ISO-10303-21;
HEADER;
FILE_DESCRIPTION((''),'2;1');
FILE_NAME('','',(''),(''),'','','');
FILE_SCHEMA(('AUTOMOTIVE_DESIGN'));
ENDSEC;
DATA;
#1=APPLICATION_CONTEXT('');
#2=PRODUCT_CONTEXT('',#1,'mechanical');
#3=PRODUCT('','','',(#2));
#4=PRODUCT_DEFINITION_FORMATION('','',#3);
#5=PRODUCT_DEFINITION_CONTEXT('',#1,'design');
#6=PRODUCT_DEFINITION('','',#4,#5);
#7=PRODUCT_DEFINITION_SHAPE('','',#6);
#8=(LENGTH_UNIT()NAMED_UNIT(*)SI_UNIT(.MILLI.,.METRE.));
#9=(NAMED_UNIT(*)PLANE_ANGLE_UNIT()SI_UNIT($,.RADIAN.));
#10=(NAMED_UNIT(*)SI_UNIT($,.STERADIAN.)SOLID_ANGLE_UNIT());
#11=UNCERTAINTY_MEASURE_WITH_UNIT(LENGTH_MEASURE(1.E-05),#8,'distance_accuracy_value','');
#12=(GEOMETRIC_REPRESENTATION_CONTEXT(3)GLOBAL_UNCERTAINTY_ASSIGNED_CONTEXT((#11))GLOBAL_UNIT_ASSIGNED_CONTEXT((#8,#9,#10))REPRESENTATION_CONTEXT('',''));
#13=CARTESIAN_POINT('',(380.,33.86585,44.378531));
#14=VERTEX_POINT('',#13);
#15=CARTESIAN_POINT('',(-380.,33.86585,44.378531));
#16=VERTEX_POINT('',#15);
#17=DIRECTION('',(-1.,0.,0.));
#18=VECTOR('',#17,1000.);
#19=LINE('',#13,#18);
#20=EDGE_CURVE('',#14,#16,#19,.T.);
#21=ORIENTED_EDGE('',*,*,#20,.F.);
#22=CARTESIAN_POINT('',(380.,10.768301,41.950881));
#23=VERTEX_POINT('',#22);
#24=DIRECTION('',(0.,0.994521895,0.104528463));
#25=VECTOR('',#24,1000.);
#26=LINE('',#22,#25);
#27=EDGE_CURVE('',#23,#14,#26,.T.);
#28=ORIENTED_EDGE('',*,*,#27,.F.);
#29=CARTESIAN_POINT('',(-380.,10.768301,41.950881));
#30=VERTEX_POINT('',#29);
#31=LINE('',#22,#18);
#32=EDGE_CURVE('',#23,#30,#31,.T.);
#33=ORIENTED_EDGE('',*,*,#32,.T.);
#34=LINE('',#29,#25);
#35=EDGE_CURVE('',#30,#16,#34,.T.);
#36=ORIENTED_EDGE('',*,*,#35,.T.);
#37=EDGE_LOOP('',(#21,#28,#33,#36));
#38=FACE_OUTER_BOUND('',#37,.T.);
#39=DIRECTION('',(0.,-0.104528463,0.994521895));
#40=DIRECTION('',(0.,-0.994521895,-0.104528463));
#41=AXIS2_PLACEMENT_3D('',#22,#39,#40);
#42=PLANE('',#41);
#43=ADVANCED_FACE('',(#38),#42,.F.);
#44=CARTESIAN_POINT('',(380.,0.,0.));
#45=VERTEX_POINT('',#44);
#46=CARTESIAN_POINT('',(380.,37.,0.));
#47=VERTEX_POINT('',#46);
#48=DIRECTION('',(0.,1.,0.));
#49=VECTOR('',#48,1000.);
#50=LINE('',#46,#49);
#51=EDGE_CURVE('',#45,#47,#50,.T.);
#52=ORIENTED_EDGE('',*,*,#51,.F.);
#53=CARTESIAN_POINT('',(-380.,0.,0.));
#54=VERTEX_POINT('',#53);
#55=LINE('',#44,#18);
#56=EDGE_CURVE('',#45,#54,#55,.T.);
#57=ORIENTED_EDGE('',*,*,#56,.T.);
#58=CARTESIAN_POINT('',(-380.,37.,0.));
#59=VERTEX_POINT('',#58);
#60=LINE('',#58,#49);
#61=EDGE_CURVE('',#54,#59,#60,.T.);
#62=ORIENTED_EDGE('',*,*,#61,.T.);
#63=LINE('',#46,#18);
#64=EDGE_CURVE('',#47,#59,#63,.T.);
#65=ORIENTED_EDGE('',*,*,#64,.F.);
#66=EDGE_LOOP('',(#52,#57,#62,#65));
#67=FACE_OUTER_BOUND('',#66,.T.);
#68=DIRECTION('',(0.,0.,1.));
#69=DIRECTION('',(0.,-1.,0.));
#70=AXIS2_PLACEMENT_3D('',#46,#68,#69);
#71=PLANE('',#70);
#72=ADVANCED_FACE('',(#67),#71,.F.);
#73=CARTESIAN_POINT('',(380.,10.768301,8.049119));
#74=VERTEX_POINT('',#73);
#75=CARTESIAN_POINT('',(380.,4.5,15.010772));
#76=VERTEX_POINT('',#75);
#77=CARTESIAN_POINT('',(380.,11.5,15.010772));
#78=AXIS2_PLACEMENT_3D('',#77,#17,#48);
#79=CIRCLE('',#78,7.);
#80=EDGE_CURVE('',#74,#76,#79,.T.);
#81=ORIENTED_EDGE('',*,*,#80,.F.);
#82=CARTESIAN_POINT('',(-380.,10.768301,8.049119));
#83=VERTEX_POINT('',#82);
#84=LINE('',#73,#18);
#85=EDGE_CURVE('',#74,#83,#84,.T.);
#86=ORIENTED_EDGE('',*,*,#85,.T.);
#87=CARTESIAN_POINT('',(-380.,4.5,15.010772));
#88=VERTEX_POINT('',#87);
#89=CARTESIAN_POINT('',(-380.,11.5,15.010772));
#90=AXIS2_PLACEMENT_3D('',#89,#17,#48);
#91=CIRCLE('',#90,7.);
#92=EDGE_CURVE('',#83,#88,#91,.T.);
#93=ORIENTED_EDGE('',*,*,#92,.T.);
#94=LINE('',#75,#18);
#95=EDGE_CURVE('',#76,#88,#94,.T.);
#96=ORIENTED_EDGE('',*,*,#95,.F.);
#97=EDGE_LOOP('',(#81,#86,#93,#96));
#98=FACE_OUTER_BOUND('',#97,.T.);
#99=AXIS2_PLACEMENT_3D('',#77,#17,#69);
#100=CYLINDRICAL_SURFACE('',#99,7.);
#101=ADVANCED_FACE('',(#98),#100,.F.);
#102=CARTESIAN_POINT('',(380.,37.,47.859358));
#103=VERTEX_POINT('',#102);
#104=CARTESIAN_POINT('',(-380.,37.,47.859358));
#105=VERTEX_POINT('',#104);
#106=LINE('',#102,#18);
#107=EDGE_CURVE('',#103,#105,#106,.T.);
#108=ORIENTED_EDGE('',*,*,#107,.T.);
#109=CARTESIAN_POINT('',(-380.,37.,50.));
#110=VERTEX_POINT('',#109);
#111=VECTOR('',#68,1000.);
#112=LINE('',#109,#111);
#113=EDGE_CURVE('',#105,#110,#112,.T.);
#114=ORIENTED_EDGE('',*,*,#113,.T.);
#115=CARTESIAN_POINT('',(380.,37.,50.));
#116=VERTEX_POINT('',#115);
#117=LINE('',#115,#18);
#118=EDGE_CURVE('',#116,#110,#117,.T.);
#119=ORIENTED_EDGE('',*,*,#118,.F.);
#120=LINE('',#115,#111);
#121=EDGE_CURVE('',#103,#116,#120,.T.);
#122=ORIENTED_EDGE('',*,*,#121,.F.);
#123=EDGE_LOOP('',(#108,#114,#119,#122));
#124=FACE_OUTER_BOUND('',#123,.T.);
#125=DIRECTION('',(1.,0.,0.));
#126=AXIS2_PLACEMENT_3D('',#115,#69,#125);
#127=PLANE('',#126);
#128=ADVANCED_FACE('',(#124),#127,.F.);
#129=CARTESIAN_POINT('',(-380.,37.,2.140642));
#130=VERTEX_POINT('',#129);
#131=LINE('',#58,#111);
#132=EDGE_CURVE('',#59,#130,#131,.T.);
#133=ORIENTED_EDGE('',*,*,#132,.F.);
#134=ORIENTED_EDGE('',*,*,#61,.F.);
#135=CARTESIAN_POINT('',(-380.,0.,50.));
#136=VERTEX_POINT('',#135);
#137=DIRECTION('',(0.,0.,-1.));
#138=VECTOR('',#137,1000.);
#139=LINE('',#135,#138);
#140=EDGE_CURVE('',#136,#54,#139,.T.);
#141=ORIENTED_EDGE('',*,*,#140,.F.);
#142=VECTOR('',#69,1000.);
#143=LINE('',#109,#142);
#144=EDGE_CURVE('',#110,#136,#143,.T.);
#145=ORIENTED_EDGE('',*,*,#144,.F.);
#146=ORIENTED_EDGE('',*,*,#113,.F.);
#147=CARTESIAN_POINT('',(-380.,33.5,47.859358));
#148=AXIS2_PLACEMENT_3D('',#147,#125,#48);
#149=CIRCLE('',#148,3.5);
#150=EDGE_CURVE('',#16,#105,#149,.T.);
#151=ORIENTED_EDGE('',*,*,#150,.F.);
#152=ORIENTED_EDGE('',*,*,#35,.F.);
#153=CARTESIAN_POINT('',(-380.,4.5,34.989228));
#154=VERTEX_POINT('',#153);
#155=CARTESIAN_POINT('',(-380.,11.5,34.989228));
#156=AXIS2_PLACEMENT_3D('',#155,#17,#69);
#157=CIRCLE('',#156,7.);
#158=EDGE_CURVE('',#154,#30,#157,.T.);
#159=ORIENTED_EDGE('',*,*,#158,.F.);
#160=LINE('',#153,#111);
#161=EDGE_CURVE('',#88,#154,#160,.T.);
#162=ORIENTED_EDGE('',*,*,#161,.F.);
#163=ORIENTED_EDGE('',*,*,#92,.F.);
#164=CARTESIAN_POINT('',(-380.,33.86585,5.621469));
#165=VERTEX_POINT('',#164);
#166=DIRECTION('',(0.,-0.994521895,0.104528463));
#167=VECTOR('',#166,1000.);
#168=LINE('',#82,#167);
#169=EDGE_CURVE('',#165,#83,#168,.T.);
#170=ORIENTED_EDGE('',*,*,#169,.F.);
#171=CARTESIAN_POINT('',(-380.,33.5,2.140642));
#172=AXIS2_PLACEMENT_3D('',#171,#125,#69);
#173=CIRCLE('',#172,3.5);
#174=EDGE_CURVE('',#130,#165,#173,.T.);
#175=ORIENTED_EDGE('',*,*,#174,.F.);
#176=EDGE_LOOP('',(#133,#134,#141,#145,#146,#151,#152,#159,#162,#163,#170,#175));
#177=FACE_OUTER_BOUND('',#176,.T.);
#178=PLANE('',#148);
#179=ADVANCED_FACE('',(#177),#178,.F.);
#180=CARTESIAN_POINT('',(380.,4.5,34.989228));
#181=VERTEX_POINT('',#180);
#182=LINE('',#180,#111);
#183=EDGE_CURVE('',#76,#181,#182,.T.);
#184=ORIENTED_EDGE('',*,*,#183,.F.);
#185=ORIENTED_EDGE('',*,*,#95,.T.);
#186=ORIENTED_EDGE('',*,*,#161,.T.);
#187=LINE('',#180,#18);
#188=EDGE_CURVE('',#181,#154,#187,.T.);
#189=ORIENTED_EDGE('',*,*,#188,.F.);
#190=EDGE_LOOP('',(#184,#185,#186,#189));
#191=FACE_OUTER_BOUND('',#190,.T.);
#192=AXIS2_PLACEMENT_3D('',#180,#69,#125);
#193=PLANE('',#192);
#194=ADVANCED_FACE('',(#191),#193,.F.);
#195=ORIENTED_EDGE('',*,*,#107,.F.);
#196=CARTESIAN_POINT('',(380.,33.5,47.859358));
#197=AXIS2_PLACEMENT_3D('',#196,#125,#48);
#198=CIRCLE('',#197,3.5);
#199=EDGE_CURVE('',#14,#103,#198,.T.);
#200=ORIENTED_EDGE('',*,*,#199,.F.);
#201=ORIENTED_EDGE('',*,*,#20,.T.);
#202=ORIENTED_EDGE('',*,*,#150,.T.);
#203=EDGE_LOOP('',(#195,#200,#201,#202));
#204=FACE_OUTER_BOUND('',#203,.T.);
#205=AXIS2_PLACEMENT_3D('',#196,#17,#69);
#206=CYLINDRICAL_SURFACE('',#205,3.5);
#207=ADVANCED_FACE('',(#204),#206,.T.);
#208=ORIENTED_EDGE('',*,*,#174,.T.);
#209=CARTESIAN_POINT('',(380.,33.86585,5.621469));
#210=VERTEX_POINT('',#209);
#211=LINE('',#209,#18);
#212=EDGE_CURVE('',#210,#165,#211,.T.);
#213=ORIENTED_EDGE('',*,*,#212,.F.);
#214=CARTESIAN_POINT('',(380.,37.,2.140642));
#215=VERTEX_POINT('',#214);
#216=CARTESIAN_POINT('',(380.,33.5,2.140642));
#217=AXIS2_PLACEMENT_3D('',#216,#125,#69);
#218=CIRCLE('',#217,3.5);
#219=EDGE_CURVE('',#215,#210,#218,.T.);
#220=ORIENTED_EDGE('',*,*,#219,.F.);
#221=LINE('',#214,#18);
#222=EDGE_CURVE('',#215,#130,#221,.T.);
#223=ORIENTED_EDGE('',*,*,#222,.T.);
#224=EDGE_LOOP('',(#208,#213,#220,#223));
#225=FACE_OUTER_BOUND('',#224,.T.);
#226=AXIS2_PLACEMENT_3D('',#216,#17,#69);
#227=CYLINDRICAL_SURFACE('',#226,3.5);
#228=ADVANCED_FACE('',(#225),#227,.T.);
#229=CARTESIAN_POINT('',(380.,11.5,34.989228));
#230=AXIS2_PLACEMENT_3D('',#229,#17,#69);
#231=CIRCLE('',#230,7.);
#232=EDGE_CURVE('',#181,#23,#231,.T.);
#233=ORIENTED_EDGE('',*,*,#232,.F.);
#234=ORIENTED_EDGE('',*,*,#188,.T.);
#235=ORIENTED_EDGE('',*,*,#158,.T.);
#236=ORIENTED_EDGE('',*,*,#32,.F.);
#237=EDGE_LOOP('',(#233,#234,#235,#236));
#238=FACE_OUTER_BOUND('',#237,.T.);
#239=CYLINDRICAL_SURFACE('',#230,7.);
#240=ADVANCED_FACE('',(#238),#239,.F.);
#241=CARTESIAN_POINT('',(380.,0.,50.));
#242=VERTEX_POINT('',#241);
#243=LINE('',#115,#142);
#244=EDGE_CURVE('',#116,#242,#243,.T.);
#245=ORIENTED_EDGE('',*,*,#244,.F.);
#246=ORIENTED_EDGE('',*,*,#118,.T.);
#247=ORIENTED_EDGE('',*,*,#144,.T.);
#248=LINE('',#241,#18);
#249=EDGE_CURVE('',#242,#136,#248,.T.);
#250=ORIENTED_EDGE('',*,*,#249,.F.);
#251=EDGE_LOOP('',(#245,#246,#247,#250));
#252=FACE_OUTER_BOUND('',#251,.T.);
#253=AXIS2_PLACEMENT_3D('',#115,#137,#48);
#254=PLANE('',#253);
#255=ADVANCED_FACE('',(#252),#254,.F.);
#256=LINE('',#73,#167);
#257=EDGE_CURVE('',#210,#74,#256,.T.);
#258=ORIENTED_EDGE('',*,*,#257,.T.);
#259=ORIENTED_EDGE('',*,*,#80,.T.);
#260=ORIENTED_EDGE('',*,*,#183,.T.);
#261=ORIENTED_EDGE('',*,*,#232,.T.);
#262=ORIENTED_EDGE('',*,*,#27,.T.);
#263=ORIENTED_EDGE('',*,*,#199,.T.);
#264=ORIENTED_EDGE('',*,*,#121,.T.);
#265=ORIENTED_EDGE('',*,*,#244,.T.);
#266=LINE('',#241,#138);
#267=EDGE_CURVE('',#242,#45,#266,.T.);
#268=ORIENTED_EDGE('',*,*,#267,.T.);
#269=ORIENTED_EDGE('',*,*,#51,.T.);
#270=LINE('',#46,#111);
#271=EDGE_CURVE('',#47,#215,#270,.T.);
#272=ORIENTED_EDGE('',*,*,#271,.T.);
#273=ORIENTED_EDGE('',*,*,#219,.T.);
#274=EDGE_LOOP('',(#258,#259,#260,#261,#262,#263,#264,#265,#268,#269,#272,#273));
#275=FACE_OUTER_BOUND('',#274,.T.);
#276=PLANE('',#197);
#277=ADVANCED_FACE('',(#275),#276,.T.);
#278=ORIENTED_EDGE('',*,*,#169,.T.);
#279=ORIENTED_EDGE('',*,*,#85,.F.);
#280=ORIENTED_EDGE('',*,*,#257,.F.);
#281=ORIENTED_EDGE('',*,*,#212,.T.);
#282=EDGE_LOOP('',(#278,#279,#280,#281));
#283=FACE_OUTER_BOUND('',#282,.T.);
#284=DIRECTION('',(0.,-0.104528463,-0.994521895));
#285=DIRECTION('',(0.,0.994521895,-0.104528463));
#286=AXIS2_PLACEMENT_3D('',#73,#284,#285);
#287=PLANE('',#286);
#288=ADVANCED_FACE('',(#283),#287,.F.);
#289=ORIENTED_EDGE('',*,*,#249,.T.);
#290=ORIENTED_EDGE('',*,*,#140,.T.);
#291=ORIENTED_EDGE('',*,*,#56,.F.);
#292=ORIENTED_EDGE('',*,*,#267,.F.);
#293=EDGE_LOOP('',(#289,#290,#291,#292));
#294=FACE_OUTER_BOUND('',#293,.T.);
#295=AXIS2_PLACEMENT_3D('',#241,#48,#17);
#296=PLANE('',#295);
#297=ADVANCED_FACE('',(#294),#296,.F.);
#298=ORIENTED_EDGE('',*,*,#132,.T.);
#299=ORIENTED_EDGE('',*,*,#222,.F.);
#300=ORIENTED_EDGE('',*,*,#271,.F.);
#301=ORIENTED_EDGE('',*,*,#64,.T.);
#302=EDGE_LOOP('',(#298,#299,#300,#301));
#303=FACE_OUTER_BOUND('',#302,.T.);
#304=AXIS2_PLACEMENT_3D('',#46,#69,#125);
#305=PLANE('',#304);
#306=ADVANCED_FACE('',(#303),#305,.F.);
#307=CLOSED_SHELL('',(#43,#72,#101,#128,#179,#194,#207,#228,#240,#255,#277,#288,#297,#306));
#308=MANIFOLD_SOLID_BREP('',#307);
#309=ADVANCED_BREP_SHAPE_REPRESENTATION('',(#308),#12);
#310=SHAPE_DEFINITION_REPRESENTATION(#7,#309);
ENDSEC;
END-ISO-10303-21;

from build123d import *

# Parameters (mm, degrees)
GB_T_707_1988_HOT_ROLLED_CHANNEL_05_1_DEPTH = 760


with BuildPart() as part:
    # Sketch1 → GB/T 707-1988 hot-rolled channel 05(1) (new body)
    with BuildSketch(Plane.YZ.offset(-380)):
        with BuildLine():
            Line((37, 50), (0, 50))
            Line((0, 50), (0, 0))
            Line((0, 0), (37, 0))
            Line((37, 0), (37, 2.140642022))
            ThreePointArc((37, 2.140642022), (36.101006889, 4.482599144), (33.865849621, 5.621468656))
            Line((33.865849621, 5.621468656), (10.768300757, 8.049118866))
            ThreePointArc((10.768300757, 8.049118866), (6.297986222, 10.326857889), (4.5, 15.010772133))
            Line((4.5, 15.010772133), (4.5, 34.989227867))
            ThreePointArc((4.5, 34.989227867), (6.297986222, 39.673142111), (10.768300757, 41.950881134))
            Line((10.768300757, 41.950881134), (33.865849621, 44.378531344))
            ThreePointArc((33.865849621, 44.378531344), (36.101006889, 45.517400856), (37, 47.859357978))
            Line((37, 47.859357978), (37, 50))
        make_face()
    extrude(amount=GB_T_707_1988_HOT_ROLLED_CHANNEL_05_1_DEPTH)


solid = part.part
